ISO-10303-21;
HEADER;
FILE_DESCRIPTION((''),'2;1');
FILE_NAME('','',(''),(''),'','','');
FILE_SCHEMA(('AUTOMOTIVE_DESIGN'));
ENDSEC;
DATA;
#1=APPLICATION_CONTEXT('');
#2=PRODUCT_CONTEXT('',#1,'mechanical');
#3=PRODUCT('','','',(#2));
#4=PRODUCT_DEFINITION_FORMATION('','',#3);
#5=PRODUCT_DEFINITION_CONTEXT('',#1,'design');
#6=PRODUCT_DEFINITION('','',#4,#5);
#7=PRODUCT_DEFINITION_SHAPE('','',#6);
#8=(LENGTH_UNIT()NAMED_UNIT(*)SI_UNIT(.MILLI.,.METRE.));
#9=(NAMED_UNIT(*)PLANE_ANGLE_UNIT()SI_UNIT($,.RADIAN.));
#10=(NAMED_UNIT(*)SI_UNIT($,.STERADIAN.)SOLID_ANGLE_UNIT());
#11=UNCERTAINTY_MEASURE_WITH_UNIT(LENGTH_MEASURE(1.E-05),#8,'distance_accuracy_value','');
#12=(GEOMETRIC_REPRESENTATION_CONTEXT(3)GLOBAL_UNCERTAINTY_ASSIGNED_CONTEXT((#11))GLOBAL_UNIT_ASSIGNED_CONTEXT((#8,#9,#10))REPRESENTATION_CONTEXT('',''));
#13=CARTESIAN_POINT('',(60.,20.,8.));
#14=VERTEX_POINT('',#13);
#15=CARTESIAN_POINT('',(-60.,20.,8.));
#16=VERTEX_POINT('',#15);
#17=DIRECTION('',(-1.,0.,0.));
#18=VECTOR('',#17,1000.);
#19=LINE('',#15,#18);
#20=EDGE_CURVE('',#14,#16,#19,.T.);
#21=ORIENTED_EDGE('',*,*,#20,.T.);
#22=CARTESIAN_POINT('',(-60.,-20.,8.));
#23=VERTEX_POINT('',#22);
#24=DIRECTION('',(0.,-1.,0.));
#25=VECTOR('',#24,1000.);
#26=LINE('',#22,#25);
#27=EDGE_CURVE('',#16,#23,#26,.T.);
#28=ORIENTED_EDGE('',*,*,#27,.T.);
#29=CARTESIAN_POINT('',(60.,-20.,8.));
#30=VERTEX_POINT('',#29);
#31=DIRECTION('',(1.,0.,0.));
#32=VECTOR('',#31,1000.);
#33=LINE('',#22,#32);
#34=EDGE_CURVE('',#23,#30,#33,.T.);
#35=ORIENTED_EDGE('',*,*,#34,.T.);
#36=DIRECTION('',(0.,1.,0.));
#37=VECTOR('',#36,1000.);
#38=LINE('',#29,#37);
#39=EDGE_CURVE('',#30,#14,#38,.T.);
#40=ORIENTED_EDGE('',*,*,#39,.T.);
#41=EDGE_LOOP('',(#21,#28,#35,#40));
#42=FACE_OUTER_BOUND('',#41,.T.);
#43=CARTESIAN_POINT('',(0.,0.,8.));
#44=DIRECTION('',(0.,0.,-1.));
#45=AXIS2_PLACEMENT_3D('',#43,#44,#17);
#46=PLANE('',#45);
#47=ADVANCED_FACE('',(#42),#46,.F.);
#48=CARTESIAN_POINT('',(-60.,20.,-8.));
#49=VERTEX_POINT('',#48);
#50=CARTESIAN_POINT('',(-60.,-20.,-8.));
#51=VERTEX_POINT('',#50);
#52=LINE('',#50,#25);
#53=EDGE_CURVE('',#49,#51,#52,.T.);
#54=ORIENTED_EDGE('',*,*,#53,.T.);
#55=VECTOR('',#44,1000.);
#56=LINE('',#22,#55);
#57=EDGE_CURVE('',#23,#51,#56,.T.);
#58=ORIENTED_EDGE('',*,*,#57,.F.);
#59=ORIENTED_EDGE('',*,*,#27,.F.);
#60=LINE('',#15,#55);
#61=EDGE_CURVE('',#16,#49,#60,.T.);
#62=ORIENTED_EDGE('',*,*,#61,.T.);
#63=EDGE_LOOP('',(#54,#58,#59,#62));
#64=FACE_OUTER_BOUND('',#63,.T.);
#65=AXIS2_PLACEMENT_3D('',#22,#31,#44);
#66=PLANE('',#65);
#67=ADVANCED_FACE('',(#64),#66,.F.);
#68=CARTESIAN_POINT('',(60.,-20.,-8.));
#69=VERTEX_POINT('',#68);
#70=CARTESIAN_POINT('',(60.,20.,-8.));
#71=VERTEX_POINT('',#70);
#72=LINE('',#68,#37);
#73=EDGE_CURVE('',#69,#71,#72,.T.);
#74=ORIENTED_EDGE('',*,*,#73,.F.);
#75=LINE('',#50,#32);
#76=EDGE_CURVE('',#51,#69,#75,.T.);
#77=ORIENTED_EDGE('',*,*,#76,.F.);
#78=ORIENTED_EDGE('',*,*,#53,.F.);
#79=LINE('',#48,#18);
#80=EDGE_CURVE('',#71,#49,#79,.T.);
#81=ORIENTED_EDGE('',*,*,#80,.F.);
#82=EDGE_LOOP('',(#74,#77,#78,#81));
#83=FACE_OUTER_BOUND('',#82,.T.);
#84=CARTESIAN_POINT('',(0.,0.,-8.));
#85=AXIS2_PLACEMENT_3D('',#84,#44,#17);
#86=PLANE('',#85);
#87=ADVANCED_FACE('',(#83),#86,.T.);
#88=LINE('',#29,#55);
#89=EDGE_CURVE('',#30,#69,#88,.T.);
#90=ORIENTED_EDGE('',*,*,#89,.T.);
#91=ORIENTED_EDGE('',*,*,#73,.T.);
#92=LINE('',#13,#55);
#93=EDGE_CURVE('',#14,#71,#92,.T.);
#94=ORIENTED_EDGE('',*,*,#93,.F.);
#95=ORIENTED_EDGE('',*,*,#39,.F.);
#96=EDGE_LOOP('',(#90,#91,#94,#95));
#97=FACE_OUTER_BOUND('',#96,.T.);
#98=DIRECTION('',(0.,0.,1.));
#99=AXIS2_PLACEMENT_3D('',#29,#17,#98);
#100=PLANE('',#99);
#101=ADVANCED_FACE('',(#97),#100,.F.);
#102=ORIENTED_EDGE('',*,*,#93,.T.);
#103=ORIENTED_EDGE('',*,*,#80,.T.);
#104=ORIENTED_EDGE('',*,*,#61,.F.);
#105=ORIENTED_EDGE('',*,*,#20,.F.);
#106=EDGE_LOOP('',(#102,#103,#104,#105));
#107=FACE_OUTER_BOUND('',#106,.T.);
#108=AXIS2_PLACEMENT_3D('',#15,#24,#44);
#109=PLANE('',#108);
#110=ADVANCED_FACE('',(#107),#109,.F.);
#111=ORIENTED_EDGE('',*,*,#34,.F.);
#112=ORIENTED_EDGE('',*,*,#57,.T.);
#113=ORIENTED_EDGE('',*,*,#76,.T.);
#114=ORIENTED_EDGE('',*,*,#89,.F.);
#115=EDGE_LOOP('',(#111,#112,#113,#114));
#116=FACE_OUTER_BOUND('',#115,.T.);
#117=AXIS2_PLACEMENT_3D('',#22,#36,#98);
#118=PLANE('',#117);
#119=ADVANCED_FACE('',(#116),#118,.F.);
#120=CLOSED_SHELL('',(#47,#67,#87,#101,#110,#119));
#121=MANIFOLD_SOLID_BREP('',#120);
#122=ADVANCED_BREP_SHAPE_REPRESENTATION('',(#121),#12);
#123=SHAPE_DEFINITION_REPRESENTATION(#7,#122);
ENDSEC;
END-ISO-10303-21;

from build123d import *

# Parameters (mm, degrees)
SKETCH1_W           = 120
SKETCH1_H           = 40
BOSS_EXTRUDE1_DEPTH = 8


with BuildPart() as part:
    # Sketch1 → Boss-Extrude1 (new, symmetric)
    with BuildSketch(Plane.XY):
        Rectangle(SKETCH1_W, SKETCH1_H)
    extrude(amount=BOSS_EXTRUDE1_DEPTH, both=True)


solid = part.part
